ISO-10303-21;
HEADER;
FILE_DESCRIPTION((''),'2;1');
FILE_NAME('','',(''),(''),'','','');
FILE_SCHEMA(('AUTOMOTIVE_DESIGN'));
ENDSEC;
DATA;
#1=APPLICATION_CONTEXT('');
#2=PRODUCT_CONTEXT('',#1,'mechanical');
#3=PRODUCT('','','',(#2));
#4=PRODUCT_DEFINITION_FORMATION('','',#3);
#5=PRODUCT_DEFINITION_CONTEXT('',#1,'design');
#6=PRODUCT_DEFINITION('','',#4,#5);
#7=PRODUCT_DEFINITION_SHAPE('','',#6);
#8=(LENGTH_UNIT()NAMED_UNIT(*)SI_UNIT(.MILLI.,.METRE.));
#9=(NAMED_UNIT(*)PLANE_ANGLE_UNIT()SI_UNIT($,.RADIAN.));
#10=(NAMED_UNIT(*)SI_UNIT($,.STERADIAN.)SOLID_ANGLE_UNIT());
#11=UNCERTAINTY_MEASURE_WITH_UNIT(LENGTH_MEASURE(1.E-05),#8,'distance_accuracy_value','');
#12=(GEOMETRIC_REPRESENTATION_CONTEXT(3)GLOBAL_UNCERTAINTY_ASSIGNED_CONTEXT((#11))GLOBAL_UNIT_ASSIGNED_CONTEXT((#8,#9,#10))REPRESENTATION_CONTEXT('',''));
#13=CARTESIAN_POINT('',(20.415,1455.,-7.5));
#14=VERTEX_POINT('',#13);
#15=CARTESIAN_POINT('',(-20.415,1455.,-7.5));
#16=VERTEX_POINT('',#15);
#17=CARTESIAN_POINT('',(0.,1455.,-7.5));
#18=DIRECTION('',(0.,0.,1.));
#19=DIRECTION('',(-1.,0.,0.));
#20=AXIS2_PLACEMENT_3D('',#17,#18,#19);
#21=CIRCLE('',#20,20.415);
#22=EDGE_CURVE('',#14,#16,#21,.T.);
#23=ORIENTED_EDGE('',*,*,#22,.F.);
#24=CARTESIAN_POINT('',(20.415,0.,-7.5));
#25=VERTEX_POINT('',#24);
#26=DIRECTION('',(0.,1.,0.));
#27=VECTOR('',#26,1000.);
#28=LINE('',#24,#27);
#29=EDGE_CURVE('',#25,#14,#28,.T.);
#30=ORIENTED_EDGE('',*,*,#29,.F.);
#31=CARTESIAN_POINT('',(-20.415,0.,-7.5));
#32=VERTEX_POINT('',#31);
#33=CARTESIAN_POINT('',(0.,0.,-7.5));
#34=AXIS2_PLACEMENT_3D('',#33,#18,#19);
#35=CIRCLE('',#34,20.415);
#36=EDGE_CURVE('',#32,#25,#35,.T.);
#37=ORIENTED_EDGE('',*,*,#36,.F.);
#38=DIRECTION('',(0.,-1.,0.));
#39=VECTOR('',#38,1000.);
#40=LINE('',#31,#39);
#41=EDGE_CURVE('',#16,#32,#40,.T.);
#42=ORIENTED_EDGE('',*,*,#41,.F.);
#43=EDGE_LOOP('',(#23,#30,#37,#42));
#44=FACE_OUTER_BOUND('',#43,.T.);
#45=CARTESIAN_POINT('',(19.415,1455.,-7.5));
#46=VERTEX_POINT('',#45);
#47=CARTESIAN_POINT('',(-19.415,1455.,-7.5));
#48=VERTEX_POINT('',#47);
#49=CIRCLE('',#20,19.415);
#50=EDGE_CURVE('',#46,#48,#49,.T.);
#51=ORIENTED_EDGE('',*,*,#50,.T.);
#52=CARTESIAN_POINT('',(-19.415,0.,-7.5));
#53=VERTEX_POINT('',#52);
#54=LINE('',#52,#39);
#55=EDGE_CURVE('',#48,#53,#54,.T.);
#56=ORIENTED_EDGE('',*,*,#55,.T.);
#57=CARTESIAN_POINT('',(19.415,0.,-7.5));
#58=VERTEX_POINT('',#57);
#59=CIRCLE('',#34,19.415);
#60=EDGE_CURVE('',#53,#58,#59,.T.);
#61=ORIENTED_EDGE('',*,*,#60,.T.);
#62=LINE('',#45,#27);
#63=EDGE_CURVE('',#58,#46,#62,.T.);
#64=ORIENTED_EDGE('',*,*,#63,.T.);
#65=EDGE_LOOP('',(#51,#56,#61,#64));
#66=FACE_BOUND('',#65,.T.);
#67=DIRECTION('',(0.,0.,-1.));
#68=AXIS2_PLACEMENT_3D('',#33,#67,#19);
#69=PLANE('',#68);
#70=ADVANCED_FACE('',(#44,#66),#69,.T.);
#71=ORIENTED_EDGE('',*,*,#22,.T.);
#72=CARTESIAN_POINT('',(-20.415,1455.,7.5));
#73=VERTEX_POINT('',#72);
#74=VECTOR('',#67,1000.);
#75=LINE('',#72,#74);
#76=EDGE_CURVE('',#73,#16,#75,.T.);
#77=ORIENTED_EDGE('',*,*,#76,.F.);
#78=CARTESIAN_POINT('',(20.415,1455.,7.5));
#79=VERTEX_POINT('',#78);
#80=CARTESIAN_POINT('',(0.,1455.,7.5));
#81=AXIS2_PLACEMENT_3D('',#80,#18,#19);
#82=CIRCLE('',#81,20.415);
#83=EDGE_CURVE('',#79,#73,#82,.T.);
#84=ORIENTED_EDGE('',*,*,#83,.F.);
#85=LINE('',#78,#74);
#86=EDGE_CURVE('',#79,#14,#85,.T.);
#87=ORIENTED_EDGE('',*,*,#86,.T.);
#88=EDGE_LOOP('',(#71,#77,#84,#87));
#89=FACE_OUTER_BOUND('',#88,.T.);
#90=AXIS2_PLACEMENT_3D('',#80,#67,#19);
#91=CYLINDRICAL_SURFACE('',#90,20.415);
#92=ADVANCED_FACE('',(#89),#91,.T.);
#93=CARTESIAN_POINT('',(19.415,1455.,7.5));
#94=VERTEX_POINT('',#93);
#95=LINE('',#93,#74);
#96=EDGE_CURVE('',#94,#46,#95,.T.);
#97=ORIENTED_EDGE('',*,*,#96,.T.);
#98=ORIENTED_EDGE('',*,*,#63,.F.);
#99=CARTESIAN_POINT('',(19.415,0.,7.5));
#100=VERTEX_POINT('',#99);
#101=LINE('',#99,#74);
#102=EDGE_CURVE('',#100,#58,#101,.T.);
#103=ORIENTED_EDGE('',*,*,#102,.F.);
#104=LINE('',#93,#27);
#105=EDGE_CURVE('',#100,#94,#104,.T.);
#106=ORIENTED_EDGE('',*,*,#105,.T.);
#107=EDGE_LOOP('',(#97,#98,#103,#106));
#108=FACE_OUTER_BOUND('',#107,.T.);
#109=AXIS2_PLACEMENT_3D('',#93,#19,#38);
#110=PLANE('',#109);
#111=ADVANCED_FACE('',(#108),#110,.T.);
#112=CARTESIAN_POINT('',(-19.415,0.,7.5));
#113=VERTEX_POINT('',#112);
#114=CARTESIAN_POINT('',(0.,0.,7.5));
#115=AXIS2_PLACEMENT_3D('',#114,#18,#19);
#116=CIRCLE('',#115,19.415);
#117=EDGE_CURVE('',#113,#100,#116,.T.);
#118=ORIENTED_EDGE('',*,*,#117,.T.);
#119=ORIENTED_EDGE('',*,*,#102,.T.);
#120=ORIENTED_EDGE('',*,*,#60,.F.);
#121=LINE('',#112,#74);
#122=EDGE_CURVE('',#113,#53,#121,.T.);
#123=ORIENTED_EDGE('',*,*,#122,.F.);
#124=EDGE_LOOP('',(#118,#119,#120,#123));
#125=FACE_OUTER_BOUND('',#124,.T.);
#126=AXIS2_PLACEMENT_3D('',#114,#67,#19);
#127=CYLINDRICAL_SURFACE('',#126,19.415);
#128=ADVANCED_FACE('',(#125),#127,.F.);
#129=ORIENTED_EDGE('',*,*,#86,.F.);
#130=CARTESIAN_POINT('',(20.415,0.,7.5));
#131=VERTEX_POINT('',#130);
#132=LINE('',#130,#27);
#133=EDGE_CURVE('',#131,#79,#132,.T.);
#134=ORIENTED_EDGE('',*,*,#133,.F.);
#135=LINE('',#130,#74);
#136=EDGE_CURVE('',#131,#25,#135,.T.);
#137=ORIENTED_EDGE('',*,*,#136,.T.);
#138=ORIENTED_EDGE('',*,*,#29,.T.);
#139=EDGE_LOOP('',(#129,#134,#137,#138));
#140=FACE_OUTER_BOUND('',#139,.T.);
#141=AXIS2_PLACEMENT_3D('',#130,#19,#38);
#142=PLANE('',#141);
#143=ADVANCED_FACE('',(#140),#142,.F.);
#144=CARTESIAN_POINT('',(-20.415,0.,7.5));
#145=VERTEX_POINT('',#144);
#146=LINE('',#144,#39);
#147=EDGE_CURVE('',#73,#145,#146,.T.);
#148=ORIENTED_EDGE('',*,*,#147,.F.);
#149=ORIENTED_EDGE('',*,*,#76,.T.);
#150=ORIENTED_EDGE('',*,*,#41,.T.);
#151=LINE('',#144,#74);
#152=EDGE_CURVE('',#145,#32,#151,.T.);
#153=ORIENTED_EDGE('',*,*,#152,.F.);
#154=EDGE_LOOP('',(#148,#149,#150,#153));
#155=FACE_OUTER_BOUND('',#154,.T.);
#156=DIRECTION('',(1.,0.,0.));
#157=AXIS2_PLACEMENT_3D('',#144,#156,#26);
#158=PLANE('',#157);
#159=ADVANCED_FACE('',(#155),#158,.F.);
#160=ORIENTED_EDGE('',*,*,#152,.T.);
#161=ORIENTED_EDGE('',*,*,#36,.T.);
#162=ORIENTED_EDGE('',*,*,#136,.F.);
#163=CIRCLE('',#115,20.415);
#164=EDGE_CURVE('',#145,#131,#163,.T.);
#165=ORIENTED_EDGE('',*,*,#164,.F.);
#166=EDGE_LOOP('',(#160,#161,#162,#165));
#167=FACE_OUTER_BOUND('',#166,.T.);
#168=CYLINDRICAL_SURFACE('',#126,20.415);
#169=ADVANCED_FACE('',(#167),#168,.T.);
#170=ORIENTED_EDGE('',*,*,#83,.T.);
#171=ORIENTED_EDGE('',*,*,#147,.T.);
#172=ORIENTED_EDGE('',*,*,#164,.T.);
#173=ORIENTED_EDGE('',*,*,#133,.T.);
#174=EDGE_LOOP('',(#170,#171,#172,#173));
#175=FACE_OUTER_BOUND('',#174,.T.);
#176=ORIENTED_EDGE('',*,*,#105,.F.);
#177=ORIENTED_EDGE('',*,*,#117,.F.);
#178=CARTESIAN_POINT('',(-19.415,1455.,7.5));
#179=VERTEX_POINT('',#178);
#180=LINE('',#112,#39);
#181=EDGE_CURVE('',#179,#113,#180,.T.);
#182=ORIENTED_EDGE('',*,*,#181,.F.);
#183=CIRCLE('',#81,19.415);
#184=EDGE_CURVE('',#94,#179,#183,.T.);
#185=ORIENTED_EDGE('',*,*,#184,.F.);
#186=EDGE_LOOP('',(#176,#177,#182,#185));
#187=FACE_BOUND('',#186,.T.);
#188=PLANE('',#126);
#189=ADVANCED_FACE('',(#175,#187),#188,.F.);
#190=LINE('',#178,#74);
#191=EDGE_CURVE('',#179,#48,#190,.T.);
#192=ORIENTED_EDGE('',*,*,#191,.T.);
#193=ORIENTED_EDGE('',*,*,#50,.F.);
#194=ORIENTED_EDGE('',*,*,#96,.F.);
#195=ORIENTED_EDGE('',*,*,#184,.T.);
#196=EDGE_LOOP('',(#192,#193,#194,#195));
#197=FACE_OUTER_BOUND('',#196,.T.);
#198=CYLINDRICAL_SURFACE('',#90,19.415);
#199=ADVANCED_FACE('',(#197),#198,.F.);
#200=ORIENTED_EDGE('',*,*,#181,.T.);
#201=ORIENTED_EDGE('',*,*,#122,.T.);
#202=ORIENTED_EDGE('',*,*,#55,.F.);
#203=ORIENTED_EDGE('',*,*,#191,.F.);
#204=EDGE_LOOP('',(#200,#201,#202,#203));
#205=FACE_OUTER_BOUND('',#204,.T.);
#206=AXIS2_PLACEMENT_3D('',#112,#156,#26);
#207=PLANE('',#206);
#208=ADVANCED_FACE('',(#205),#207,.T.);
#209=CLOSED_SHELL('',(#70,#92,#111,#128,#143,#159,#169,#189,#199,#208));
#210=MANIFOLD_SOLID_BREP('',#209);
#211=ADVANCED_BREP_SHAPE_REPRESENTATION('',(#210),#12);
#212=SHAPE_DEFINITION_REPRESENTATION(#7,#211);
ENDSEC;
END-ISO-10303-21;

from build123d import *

# Parameters (mm, degrees)
EXTRUDE_1_DEPTH = 7.5


with BuildPart() as part:
    # 草图2 → 拉伸-薄壁1 (new, symmetric)
    with BuildSketch(Plane.XY):
        with BuildLine():
            Line((20.415, 1455), (20.415, 0))
            ThreePointArc((20.415, 0), (0, -20.415), (-20.415, 0))
            Line((-20.415, 0), (-20.415, 1455))
            ThreePointArc((-20.415, 1455), (0, 1475.415), (20.415, 1455))
        make_face()
        with BuildLine():
            Line((19.415, 1455), (19.415, 0))
            ThreePointArc((19.415, 0), (0, -19.415), (-19.415, 0))
            Line((-19.415, 0), (-19.415, 1455))
            ThreePointArc((-19.415, 1455), (0, 1474.415), (19.415, 1455))
        make_face(mode=Mode.SUBTRACT)
    extrude(amount=EXTRUDE_1_DEPTH, both=True)


solid = part.part
